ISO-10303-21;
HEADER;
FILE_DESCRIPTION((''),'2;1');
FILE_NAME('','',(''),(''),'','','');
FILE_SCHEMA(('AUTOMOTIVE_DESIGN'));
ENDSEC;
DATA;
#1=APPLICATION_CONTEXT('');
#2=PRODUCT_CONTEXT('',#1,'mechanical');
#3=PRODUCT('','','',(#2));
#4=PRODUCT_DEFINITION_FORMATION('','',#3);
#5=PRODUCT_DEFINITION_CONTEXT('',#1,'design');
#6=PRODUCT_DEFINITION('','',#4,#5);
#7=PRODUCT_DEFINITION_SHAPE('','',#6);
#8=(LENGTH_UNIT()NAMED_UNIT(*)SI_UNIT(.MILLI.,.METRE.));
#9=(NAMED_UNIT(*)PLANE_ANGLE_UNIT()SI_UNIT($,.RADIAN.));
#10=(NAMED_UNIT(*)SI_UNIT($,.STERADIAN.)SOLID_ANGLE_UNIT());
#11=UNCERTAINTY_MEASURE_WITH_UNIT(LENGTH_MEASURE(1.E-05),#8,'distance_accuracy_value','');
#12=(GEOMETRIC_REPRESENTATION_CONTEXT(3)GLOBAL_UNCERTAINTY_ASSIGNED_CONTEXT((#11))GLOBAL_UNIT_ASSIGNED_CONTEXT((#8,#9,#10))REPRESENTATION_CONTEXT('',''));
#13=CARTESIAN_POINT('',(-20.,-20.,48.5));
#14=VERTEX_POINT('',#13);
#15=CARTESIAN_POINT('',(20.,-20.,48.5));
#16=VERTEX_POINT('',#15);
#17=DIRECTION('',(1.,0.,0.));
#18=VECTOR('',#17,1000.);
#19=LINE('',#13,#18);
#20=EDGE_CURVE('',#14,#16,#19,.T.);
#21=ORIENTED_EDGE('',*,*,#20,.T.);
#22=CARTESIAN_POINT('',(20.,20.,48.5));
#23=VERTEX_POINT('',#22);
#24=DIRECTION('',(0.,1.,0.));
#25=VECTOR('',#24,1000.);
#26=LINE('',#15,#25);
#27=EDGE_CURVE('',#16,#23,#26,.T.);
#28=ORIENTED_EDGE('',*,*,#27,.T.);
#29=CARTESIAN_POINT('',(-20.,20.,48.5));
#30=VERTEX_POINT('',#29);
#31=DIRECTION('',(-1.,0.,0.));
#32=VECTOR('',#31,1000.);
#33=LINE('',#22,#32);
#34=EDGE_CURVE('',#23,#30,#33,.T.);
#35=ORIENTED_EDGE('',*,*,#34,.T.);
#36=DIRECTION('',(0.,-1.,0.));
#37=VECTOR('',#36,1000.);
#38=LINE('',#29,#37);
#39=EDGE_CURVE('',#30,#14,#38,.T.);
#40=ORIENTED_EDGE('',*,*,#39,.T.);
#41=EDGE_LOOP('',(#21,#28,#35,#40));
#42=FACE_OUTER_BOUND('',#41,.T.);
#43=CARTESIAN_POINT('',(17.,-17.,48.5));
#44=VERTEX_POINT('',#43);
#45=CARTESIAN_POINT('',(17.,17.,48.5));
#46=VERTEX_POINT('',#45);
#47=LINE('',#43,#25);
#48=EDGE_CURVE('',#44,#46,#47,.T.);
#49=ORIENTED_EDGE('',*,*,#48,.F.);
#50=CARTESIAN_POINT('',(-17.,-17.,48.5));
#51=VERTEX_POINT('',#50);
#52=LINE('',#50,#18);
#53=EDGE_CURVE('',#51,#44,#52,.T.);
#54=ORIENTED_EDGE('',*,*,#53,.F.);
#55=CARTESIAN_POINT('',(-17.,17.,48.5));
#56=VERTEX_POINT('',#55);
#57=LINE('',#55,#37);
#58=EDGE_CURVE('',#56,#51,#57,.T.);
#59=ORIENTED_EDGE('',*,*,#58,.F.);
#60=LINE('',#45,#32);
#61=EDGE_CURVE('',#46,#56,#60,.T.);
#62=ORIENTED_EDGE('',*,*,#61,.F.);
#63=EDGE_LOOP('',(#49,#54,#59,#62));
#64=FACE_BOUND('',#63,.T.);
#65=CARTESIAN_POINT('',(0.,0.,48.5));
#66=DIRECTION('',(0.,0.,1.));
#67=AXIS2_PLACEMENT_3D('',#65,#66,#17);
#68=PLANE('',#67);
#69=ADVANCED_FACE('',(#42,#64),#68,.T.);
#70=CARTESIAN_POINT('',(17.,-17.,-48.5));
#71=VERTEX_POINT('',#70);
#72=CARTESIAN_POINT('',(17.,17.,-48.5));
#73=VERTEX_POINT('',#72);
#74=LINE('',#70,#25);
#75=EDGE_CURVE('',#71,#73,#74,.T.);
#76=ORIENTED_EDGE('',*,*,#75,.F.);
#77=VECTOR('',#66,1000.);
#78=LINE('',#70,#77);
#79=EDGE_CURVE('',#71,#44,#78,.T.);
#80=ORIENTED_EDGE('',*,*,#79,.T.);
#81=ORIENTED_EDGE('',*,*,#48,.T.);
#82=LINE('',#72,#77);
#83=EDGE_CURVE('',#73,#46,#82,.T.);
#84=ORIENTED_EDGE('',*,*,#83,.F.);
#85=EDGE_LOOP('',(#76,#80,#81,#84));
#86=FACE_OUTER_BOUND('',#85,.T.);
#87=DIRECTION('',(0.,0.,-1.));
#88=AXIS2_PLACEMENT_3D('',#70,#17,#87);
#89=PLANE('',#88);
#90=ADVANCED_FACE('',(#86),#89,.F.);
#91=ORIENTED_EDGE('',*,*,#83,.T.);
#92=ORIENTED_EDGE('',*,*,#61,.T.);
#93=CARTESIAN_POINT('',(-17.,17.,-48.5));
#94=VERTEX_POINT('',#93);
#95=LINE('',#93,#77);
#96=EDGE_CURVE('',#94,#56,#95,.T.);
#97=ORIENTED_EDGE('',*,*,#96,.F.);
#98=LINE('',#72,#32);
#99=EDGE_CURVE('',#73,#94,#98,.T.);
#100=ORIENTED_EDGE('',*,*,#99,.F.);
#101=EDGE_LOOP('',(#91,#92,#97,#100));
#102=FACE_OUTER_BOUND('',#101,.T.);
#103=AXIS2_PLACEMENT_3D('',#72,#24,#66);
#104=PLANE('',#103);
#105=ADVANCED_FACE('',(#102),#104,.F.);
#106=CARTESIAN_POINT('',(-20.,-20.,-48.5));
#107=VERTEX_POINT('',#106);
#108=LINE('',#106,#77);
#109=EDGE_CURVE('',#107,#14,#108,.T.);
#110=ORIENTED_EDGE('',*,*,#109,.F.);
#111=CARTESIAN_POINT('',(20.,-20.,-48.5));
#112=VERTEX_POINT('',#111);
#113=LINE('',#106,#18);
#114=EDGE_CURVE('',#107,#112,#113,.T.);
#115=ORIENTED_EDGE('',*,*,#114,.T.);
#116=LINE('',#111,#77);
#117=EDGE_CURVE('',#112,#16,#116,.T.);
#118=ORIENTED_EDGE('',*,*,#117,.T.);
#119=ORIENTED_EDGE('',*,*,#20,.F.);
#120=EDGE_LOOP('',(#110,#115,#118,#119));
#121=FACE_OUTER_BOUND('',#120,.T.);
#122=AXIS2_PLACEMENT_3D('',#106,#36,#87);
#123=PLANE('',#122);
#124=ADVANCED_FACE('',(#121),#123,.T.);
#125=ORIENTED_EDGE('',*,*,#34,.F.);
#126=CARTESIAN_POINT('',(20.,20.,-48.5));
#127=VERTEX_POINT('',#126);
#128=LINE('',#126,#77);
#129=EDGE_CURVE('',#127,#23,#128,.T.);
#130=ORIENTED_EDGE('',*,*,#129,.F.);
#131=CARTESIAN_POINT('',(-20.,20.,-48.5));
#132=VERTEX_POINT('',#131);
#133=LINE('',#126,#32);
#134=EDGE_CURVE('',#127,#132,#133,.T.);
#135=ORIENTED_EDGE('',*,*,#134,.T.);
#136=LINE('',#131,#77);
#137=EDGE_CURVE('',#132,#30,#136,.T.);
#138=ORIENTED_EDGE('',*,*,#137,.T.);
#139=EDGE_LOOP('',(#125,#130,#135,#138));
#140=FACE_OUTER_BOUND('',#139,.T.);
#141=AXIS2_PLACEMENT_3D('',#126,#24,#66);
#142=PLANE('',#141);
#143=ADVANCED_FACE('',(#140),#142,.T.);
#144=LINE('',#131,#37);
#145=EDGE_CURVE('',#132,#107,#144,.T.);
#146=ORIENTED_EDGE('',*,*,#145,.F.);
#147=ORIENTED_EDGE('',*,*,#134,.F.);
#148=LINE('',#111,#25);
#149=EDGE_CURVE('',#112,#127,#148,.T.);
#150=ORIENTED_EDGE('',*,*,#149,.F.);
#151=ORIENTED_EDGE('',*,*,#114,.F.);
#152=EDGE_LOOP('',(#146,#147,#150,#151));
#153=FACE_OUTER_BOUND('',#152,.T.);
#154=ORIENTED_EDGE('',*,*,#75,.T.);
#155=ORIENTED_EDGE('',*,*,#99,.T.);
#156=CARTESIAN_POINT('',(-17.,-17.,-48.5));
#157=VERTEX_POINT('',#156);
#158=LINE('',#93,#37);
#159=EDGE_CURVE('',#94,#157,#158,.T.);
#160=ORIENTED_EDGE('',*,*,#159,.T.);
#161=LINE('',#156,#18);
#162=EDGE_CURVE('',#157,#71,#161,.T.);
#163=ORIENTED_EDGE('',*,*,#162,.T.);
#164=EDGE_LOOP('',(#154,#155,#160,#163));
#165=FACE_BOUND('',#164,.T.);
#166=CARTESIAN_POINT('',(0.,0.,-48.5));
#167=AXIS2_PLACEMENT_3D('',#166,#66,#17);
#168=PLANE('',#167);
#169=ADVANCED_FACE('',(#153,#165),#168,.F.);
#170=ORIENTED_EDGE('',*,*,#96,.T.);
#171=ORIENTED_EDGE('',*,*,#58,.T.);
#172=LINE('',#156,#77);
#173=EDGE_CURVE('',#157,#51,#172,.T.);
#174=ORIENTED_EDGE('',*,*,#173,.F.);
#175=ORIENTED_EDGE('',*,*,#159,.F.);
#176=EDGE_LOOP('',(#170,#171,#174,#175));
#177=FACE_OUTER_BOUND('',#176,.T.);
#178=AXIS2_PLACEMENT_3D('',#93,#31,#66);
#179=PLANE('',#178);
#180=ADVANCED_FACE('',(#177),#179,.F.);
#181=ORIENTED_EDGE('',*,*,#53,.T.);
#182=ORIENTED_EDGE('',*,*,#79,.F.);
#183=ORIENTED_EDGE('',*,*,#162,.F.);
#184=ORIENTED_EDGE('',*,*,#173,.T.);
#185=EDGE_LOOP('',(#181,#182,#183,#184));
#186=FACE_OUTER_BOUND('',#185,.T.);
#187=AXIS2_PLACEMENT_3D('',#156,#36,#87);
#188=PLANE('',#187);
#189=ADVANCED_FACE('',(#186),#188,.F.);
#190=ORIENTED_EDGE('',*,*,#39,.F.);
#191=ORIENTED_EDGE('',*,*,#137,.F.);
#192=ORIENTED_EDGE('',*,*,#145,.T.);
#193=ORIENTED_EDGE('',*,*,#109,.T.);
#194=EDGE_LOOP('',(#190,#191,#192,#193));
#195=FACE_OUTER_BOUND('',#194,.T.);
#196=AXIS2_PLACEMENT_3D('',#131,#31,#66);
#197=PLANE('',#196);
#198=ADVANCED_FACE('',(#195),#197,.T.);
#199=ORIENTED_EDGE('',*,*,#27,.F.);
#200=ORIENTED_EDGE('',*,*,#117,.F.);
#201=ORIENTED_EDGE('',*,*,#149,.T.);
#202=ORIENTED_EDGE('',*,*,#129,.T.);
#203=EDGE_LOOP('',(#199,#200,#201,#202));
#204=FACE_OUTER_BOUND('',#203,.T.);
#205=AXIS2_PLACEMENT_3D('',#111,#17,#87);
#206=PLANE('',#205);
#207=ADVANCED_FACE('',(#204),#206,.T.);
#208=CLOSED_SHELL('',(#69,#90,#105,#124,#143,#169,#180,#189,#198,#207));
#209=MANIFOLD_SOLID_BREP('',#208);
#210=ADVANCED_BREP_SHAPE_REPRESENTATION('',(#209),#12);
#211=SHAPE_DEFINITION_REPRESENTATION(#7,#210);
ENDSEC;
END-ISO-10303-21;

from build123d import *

# Parameters (mm, degrees)
SKETCH_1_W      = 40
SKETCH_1_H      = 40
SKETCH_1_W_2    = 34
SKETCH_1_H_2    = 34
EXTRUDE_1_DEPTH = 48.5


with BuildPart() as part:
    # 草图1 → 凸台-拉伸1 (new, symmetric)
    with BuildSketch(Plane.XY):
        Rectangle(SKETCH_1_W, SKETCH_1_H)
        Rectangle(SKETCH_1_W_2, SKETCH_1_H_2, mode=Mode.SUBTRACT)
    extrude(amount=EXTRUDE_1_DEPTH, both=True)


solid = part.part
